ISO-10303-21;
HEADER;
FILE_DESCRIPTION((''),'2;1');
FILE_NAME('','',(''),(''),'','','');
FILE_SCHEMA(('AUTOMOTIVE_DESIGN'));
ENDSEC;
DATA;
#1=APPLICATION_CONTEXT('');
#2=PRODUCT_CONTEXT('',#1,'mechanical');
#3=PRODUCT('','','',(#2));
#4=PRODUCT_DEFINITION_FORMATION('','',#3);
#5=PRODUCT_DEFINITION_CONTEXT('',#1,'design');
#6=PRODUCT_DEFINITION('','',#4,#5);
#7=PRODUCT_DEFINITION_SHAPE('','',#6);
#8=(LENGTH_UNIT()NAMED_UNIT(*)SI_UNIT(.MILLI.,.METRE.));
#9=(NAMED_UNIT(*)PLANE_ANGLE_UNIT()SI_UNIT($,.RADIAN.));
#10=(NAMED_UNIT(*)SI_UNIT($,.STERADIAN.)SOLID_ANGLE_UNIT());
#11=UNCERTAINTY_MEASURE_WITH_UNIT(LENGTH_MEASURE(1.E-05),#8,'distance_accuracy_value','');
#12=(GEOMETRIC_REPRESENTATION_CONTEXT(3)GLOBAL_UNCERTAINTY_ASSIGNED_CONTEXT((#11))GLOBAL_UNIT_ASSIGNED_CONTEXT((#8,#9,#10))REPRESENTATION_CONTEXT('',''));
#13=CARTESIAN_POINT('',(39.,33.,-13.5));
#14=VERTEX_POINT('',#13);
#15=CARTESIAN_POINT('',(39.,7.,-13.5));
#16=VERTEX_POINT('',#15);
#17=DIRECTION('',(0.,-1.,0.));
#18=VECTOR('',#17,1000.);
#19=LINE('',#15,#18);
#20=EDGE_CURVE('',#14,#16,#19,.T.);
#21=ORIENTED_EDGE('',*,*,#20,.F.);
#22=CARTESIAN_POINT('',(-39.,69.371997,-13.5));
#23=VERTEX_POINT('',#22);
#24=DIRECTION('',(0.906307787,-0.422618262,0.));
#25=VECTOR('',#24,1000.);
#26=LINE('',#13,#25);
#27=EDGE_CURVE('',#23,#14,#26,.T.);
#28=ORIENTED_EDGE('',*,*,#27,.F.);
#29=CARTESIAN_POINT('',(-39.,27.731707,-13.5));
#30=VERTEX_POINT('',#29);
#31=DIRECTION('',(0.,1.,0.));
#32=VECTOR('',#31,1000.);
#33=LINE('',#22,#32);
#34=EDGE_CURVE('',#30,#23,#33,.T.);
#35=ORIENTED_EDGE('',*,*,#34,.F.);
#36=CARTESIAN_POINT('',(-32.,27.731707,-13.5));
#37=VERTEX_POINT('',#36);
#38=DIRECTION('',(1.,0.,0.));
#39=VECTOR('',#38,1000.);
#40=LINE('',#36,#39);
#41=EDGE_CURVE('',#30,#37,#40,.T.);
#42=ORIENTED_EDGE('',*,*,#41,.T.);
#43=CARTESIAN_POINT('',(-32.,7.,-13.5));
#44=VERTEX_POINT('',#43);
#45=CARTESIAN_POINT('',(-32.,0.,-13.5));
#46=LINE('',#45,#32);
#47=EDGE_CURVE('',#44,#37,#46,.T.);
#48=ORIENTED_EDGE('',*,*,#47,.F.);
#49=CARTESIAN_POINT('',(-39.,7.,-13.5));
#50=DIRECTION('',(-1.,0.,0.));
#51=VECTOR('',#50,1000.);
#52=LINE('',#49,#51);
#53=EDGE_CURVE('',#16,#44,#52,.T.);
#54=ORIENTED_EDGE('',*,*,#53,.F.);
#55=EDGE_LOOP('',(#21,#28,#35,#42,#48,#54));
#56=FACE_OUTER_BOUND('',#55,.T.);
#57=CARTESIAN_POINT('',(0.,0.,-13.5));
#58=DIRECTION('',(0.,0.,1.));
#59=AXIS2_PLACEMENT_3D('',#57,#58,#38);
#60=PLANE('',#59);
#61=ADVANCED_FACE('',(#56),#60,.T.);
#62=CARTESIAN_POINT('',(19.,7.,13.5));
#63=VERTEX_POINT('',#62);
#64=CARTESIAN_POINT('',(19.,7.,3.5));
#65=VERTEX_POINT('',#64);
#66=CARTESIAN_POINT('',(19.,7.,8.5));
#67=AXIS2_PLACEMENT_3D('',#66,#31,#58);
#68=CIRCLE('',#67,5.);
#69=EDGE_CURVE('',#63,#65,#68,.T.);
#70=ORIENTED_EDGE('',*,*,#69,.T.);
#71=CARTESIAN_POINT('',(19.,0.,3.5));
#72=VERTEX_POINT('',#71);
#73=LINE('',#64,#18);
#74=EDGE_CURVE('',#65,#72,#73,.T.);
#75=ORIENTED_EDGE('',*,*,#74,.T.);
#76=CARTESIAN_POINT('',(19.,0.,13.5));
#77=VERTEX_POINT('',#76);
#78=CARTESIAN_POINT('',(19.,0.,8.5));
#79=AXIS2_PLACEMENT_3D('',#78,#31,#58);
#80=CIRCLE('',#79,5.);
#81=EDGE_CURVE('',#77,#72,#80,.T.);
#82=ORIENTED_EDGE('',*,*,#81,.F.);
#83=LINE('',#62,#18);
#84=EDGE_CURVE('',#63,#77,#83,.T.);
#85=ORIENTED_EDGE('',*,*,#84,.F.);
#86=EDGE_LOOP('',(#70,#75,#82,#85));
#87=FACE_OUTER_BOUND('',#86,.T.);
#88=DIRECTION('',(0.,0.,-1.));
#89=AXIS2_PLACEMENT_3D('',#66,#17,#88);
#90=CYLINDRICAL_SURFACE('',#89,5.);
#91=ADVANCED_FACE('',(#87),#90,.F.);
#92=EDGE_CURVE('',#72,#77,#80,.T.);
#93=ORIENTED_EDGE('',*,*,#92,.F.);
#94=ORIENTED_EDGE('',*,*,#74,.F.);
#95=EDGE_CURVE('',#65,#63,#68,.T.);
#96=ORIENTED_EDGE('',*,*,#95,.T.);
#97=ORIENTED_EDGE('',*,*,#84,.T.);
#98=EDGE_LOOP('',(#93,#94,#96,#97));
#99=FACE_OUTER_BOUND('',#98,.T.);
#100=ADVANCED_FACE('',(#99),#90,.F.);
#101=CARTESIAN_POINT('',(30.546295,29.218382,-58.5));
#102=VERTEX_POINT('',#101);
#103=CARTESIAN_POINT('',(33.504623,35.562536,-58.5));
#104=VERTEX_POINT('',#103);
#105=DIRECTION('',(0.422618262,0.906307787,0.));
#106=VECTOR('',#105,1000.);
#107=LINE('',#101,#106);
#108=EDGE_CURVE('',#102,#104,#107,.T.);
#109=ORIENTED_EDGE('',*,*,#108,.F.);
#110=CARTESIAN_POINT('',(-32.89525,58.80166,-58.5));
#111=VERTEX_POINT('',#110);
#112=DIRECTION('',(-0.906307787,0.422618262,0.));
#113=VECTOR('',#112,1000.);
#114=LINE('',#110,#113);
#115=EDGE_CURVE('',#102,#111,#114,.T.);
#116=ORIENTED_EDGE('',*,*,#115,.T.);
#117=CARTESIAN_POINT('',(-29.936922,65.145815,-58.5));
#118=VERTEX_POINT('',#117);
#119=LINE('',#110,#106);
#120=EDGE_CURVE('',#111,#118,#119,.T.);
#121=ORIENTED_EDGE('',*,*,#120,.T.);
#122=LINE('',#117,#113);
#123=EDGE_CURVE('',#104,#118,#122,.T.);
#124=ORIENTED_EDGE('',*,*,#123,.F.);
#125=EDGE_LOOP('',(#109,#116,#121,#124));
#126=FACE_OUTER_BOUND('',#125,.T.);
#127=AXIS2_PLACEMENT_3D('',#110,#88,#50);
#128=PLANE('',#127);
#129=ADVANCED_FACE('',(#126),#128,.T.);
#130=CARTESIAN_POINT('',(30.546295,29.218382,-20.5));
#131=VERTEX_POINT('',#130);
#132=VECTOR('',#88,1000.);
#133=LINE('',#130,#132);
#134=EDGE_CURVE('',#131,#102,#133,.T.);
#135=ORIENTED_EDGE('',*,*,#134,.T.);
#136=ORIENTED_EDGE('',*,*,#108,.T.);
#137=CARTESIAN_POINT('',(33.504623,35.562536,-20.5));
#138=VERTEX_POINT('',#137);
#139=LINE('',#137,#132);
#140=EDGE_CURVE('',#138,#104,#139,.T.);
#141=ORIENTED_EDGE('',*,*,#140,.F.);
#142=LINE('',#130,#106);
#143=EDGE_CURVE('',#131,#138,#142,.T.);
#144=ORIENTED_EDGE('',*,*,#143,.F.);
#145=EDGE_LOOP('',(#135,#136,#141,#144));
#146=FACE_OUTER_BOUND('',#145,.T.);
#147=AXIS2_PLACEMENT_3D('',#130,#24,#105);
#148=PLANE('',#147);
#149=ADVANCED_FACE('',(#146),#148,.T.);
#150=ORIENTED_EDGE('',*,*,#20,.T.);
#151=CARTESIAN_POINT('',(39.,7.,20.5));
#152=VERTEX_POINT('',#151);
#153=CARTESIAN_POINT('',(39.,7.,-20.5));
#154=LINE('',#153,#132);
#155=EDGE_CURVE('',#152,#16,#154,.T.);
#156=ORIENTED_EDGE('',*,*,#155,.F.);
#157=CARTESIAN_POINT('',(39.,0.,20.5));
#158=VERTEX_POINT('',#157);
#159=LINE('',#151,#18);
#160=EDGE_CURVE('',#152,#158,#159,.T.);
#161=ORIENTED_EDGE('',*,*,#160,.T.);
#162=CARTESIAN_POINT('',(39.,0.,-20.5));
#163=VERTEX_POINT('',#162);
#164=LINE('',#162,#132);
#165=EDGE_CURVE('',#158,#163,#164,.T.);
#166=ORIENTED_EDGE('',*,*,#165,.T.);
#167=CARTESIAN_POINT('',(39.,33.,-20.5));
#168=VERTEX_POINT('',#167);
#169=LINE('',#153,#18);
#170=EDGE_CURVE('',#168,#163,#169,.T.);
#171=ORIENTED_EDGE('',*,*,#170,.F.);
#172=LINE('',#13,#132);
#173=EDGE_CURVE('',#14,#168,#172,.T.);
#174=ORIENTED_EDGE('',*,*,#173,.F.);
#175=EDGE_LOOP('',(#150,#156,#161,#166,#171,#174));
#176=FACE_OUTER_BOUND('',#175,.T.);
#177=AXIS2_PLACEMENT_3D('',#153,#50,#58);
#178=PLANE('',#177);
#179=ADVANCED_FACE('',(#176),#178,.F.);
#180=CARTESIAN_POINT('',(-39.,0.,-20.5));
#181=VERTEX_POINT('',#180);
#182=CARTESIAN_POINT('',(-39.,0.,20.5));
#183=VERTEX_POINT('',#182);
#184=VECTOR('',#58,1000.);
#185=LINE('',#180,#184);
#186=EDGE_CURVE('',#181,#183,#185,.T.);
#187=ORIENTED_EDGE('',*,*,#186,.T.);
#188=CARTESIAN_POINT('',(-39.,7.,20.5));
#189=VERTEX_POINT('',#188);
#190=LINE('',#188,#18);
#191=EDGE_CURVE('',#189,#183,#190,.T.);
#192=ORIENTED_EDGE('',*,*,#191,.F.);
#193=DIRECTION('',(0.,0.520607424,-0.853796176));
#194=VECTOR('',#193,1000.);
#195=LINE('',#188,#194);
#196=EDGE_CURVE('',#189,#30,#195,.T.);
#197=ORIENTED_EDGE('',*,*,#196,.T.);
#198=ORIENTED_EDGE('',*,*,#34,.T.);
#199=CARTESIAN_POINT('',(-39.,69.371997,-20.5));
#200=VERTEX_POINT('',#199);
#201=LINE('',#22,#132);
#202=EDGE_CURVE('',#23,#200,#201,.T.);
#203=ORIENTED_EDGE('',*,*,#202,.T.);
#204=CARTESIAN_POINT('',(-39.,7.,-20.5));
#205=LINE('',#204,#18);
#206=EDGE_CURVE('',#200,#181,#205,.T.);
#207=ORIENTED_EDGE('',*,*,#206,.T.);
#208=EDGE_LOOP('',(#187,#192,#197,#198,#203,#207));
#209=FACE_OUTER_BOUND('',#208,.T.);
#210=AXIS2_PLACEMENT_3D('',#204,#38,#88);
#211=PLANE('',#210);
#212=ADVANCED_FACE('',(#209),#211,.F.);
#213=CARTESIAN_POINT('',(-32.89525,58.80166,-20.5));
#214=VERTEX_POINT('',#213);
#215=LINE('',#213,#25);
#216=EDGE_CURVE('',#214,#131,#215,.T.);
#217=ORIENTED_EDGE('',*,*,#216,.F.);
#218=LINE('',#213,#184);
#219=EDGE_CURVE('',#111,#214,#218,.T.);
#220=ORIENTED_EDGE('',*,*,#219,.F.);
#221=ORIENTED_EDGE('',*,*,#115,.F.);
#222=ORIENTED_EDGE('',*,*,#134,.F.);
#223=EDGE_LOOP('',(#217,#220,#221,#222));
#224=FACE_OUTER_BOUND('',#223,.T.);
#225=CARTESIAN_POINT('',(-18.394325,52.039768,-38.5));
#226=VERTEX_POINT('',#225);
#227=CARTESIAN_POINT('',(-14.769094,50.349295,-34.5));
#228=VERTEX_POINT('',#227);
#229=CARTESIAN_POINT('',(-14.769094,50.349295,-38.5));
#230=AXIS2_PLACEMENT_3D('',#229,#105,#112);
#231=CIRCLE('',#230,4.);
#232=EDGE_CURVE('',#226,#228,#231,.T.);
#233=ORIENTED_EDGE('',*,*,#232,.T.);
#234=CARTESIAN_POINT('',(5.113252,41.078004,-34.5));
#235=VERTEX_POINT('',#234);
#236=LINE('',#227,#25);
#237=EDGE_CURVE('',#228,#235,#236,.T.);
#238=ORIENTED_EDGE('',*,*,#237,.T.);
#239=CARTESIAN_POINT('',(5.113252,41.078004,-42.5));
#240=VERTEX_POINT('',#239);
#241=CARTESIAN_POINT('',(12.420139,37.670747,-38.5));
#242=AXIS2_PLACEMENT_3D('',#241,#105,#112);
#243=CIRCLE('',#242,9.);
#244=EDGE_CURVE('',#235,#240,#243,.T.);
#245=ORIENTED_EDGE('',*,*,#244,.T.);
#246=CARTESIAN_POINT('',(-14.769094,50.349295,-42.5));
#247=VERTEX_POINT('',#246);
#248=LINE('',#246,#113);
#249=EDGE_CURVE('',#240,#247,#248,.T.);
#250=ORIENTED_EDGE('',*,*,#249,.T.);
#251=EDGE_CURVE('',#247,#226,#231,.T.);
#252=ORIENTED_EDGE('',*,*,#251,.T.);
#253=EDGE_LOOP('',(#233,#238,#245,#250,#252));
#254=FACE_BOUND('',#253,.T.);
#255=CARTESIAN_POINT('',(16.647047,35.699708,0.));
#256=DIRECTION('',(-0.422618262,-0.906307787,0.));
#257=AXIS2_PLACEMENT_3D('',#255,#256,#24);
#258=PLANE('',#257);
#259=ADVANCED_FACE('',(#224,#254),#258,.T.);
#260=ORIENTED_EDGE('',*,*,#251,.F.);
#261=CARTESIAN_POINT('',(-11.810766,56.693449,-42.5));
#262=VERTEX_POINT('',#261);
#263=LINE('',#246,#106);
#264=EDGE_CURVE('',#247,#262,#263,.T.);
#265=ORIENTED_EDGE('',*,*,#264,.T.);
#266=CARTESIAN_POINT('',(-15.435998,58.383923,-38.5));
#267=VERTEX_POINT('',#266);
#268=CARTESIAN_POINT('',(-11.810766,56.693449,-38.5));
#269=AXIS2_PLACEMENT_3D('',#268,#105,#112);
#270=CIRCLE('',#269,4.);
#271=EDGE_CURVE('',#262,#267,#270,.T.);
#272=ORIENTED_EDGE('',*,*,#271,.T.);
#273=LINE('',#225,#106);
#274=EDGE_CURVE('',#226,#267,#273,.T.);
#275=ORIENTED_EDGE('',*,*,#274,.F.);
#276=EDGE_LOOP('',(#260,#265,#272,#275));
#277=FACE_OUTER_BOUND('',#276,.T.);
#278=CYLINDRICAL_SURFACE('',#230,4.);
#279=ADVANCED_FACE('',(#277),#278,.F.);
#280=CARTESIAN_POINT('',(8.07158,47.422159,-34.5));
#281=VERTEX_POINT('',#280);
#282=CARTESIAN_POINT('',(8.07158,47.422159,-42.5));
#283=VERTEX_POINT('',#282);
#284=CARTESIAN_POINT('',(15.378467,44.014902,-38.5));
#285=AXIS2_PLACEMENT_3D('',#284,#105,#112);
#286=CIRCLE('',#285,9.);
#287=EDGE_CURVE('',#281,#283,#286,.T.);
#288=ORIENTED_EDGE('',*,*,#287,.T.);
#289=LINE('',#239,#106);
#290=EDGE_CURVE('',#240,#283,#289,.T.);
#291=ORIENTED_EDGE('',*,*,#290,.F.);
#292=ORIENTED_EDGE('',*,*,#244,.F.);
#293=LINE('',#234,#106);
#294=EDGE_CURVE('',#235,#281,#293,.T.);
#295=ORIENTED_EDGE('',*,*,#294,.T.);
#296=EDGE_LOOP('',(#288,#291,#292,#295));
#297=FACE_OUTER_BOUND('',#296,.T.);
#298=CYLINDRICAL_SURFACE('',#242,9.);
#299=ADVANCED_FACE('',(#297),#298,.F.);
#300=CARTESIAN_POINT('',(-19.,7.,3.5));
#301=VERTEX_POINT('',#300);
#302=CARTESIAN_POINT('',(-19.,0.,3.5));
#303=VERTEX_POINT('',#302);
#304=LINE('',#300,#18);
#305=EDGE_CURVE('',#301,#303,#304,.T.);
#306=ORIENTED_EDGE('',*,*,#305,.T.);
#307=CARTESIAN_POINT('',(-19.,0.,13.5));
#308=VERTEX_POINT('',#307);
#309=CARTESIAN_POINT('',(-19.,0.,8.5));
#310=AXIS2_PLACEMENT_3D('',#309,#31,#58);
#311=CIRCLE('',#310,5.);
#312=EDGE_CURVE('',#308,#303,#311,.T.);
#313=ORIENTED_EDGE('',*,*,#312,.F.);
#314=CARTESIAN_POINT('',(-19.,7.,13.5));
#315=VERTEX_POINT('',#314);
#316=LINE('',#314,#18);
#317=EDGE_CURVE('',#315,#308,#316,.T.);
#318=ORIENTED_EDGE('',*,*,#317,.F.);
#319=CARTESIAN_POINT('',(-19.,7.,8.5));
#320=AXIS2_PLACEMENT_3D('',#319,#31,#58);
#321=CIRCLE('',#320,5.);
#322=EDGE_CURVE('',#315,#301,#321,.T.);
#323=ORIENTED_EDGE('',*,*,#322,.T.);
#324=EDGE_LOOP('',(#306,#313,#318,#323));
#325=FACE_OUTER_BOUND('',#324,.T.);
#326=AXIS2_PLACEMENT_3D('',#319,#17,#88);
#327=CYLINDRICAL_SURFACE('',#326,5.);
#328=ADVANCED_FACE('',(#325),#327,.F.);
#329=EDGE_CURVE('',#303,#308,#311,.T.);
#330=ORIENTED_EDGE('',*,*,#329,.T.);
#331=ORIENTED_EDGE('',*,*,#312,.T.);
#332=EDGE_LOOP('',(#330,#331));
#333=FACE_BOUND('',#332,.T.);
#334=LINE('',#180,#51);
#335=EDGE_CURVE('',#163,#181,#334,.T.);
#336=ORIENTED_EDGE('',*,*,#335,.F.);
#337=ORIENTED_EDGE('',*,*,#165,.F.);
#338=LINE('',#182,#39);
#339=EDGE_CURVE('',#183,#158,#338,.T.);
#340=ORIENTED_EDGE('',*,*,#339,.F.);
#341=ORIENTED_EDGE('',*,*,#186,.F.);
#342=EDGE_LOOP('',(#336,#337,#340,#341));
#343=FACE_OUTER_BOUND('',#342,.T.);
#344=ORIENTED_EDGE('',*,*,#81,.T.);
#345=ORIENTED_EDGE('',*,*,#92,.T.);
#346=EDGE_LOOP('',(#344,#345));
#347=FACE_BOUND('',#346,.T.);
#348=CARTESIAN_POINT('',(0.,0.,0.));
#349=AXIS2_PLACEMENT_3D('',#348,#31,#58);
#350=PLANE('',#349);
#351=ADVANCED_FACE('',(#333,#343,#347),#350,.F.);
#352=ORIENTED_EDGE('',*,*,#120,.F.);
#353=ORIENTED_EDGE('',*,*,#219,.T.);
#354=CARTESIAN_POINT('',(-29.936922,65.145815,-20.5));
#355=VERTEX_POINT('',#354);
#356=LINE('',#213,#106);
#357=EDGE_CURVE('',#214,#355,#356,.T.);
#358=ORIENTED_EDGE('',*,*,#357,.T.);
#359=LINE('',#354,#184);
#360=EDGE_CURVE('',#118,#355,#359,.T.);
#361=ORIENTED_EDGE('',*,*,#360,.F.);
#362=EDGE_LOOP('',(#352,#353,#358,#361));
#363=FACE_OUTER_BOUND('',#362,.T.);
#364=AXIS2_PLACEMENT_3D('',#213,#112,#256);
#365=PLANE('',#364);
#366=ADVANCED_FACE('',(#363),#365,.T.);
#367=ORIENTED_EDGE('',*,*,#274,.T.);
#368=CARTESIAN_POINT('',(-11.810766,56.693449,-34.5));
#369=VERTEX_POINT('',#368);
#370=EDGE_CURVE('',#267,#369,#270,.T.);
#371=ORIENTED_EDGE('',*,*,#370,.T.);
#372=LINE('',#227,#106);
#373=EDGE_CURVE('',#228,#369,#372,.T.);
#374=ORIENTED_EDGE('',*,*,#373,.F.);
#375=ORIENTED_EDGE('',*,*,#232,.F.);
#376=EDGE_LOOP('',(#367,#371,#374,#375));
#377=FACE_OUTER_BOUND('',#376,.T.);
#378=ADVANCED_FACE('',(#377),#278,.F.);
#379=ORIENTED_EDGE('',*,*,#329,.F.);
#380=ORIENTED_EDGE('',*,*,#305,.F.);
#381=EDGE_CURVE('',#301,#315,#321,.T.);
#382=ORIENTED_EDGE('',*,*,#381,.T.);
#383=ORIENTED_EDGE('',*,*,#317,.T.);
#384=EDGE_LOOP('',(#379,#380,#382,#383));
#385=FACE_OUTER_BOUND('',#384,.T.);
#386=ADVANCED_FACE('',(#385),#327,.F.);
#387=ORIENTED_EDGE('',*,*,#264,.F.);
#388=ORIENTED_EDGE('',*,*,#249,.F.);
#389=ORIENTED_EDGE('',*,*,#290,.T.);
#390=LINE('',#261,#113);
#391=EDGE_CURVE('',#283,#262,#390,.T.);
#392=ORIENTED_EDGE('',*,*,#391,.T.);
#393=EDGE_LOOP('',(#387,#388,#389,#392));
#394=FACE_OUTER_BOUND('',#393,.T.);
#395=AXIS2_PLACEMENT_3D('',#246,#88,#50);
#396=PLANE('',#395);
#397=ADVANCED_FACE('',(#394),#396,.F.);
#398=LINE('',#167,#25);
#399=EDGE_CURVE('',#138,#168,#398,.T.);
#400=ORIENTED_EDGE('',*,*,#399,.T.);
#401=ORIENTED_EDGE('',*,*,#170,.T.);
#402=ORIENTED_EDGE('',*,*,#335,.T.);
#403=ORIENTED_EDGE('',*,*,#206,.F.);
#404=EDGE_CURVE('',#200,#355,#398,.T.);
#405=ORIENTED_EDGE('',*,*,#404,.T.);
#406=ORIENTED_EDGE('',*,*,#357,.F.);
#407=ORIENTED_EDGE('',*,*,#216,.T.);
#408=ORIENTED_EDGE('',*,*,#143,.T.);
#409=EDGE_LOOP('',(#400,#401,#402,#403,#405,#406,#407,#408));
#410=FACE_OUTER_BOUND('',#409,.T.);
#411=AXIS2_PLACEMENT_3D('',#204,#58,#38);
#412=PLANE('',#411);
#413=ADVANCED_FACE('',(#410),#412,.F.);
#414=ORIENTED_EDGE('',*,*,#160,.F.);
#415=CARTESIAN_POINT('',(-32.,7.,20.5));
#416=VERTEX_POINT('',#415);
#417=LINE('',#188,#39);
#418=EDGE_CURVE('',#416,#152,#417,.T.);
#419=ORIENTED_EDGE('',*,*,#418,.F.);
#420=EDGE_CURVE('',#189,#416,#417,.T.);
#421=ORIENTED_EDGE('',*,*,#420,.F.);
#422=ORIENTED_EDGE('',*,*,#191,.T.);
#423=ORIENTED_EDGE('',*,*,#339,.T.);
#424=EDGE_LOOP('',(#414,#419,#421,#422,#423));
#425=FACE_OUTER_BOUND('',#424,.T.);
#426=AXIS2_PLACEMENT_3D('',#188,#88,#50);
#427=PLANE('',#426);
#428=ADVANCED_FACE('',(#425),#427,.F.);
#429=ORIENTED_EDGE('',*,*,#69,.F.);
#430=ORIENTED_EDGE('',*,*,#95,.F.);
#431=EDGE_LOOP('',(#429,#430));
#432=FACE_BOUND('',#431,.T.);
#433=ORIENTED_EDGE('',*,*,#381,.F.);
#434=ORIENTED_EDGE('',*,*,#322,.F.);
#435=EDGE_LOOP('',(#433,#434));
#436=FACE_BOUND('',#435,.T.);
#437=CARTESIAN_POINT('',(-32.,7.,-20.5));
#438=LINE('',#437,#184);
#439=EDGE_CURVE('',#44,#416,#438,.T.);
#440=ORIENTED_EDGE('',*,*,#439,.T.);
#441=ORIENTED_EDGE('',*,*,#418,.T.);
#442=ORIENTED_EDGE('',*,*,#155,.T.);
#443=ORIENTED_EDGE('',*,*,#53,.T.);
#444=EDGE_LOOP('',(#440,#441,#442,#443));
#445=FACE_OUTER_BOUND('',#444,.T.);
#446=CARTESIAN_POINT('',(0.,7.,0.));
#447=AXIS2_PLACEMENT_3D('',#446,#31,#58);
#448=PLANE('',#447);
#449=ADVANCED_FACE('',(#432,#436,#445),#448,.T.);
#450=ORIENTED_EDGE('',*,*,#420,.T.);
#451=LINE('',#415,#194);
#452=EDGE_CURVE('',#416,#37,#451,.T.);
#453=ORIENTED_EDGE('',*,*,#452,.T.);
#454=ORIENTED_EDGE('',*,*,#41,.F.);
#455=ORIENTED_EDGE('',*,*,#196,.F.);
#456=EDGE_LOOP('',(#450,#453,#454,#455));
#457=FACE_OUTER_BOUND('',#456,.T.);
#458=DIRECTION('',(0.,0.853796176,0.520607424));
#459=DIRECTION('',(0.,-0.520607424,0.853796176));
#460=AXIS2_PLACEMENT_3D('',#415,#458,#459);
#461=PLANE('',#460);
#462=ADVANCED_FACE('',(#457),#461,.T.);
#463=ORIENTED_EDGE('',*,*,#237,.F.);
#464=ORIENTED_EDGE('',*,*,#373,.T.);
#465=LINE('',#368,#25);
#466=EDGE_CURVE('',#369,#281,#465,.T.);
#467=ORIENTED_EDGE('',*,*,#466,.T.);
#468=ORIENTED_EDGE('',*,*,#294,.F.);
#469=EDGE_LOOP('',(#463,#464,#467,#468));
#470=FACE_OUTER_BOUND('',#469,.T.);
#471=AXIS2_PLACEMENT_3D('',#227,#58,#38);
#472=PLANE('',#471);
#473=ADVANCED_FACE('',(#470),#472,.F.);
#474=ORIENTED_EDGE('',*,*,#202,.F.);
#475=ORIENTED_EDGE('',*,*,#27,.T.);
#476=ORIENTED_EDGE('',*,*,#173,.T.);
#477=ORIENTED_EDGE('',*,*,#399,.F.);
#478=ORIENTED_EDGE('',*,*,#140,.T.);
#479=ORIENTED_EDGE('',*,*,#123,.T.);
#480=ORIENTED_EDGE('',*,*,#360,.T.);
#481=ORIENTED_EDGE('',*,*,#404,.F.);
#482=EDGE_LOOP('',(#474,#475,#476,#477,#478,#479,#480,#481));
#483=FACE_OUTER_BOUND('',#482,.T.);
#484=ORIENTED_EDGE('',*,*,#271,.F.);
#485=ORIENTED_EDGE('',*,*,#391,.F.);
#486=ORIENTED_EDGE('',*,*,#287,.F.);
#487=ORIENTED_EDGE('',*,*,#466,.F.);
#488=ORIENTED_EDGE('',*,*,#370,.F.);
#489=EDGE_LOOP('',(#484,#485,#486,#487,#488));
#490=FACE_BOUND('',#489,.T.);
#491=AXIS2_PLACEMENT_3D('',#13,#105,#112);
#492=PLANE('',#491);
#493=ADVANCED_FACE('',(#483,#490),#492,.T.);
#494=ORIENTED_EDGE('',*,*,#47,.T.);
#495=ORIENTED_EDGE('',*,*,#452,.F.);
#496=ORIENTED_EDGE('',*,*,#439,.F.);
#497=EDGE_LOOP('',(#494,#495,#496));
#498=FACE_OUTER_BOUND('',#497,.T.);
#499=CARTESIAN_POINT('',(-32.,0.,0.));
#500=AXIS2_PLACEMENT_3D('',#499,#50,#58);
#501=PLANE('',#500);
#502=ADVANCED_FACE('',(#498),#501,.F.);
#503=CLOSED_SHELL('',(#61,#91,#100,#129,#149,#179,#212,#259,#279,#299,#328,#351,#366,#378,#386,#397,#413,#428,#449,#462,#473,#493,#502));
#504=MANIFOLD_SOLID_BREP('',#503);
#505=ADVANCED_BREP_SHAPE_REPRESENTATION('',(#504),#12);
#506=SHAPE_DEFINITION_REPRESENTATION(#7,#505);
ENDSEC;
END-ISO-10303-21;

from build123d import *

# Parameters (mm, degrees)
BASE_PLATE_SKETCH_W           = 78
BASE_PLATE_SKETCH_H           = 41
BASE_PLATE_SKETCH_R           = 5
BASE_PLATE_DEPTH              = 7
GUSSET_DEPTH                  = 7
UPRIGHT_WALL_DEPTH            = 7
KEYHOLE_FLANGE_SKETCH_W       = 70
KEYHOLE_FLANGE_SKETCH_H       = 38
KEYHOLE_MOUNTING_FLANGE_DEPTH = 7


with BuildPart() as part:
    # Base Plate Sketch → Base Plate (new body)
    with BuildSketch(Plane(origin=(0, 0, 0), x_dir=(1, 0, 0), z_dir=(0, 1, 0))):
        Rectangle(BASE_PLATE_SKETCH_W, BASE_PLATE_SKETCH_H)
        with Locations(Location((-19, -8.5, 0), (0, 0, 270))):
            Circle(BASE_PLATE_SKETCH_R, mode=Mode.SUBTRACT)
        with Locations(Location((19, -8.5, 0), (0, 0, 270))):
            Circle(BASE_PLATE_SKETCH_R, mode=Mode.SUBTRACT)
    extrude(amount=BASE_PLATE_DEPTH)

    # Gusset Sketch → Gusset (add)
    with BuildSketch(Plane.ZY.offset(39)):
        Polygon((-20.5, 7), (-20.5, 32), (20.5, 7), align=None)
    extrude(amount=-GUSSET_DEPTH)

    # Upright Wall Sketch → Upright Wall (add)
    with BuildSketch(Plane(origin=(0, 0, -20.5), x_dir=(-1, 0, 0), z_dir=(0, 0, -1))):
        Polygon((-39, 7), (-39, 33), (39, 69.371997336), (39, 7), align=None)
    extrude(amount=-UPRIGHT_WALL_DEPTH)

    # Keyhole Flange Sketch → Keyhole Mounting Flange (add)
    with BuildSketch(Plane(origin=(19.605374923, 42.043862201, 0), x_dir=(0.9063077870366493, -0.4226182617407009, 0), z_dir=(0.4226182617407009, 0.9063077870366493, 0))):
        with Locations((-19.663876622, 39.5)):
            Rectangle(KEYHOLE_FLANGE_SKETCH_W, KEYHOLE_FLANGE_SKETCH_H)
        with BuildLine():
            Line((-34.663876622, 42.5), (-12.72613437, 42.5))
            ThreePointArc((-12.72613437, 42.5), (4.336123378, 38.5), (-12.72613437, 34.5))
            Line((-12.72613437, 34.5), (-34.663876622, 34.5))
            ThreePointArc((-34.663876622, 34.5), (-38.663876622, 38.5), (-34.663876622, 42.5))
        make_face(mode=Mode.SUBTRACT)
    extrude(amount=-KEYHOLE_MOUNTING_FLANGE_DEPTH)


solid = part.part
